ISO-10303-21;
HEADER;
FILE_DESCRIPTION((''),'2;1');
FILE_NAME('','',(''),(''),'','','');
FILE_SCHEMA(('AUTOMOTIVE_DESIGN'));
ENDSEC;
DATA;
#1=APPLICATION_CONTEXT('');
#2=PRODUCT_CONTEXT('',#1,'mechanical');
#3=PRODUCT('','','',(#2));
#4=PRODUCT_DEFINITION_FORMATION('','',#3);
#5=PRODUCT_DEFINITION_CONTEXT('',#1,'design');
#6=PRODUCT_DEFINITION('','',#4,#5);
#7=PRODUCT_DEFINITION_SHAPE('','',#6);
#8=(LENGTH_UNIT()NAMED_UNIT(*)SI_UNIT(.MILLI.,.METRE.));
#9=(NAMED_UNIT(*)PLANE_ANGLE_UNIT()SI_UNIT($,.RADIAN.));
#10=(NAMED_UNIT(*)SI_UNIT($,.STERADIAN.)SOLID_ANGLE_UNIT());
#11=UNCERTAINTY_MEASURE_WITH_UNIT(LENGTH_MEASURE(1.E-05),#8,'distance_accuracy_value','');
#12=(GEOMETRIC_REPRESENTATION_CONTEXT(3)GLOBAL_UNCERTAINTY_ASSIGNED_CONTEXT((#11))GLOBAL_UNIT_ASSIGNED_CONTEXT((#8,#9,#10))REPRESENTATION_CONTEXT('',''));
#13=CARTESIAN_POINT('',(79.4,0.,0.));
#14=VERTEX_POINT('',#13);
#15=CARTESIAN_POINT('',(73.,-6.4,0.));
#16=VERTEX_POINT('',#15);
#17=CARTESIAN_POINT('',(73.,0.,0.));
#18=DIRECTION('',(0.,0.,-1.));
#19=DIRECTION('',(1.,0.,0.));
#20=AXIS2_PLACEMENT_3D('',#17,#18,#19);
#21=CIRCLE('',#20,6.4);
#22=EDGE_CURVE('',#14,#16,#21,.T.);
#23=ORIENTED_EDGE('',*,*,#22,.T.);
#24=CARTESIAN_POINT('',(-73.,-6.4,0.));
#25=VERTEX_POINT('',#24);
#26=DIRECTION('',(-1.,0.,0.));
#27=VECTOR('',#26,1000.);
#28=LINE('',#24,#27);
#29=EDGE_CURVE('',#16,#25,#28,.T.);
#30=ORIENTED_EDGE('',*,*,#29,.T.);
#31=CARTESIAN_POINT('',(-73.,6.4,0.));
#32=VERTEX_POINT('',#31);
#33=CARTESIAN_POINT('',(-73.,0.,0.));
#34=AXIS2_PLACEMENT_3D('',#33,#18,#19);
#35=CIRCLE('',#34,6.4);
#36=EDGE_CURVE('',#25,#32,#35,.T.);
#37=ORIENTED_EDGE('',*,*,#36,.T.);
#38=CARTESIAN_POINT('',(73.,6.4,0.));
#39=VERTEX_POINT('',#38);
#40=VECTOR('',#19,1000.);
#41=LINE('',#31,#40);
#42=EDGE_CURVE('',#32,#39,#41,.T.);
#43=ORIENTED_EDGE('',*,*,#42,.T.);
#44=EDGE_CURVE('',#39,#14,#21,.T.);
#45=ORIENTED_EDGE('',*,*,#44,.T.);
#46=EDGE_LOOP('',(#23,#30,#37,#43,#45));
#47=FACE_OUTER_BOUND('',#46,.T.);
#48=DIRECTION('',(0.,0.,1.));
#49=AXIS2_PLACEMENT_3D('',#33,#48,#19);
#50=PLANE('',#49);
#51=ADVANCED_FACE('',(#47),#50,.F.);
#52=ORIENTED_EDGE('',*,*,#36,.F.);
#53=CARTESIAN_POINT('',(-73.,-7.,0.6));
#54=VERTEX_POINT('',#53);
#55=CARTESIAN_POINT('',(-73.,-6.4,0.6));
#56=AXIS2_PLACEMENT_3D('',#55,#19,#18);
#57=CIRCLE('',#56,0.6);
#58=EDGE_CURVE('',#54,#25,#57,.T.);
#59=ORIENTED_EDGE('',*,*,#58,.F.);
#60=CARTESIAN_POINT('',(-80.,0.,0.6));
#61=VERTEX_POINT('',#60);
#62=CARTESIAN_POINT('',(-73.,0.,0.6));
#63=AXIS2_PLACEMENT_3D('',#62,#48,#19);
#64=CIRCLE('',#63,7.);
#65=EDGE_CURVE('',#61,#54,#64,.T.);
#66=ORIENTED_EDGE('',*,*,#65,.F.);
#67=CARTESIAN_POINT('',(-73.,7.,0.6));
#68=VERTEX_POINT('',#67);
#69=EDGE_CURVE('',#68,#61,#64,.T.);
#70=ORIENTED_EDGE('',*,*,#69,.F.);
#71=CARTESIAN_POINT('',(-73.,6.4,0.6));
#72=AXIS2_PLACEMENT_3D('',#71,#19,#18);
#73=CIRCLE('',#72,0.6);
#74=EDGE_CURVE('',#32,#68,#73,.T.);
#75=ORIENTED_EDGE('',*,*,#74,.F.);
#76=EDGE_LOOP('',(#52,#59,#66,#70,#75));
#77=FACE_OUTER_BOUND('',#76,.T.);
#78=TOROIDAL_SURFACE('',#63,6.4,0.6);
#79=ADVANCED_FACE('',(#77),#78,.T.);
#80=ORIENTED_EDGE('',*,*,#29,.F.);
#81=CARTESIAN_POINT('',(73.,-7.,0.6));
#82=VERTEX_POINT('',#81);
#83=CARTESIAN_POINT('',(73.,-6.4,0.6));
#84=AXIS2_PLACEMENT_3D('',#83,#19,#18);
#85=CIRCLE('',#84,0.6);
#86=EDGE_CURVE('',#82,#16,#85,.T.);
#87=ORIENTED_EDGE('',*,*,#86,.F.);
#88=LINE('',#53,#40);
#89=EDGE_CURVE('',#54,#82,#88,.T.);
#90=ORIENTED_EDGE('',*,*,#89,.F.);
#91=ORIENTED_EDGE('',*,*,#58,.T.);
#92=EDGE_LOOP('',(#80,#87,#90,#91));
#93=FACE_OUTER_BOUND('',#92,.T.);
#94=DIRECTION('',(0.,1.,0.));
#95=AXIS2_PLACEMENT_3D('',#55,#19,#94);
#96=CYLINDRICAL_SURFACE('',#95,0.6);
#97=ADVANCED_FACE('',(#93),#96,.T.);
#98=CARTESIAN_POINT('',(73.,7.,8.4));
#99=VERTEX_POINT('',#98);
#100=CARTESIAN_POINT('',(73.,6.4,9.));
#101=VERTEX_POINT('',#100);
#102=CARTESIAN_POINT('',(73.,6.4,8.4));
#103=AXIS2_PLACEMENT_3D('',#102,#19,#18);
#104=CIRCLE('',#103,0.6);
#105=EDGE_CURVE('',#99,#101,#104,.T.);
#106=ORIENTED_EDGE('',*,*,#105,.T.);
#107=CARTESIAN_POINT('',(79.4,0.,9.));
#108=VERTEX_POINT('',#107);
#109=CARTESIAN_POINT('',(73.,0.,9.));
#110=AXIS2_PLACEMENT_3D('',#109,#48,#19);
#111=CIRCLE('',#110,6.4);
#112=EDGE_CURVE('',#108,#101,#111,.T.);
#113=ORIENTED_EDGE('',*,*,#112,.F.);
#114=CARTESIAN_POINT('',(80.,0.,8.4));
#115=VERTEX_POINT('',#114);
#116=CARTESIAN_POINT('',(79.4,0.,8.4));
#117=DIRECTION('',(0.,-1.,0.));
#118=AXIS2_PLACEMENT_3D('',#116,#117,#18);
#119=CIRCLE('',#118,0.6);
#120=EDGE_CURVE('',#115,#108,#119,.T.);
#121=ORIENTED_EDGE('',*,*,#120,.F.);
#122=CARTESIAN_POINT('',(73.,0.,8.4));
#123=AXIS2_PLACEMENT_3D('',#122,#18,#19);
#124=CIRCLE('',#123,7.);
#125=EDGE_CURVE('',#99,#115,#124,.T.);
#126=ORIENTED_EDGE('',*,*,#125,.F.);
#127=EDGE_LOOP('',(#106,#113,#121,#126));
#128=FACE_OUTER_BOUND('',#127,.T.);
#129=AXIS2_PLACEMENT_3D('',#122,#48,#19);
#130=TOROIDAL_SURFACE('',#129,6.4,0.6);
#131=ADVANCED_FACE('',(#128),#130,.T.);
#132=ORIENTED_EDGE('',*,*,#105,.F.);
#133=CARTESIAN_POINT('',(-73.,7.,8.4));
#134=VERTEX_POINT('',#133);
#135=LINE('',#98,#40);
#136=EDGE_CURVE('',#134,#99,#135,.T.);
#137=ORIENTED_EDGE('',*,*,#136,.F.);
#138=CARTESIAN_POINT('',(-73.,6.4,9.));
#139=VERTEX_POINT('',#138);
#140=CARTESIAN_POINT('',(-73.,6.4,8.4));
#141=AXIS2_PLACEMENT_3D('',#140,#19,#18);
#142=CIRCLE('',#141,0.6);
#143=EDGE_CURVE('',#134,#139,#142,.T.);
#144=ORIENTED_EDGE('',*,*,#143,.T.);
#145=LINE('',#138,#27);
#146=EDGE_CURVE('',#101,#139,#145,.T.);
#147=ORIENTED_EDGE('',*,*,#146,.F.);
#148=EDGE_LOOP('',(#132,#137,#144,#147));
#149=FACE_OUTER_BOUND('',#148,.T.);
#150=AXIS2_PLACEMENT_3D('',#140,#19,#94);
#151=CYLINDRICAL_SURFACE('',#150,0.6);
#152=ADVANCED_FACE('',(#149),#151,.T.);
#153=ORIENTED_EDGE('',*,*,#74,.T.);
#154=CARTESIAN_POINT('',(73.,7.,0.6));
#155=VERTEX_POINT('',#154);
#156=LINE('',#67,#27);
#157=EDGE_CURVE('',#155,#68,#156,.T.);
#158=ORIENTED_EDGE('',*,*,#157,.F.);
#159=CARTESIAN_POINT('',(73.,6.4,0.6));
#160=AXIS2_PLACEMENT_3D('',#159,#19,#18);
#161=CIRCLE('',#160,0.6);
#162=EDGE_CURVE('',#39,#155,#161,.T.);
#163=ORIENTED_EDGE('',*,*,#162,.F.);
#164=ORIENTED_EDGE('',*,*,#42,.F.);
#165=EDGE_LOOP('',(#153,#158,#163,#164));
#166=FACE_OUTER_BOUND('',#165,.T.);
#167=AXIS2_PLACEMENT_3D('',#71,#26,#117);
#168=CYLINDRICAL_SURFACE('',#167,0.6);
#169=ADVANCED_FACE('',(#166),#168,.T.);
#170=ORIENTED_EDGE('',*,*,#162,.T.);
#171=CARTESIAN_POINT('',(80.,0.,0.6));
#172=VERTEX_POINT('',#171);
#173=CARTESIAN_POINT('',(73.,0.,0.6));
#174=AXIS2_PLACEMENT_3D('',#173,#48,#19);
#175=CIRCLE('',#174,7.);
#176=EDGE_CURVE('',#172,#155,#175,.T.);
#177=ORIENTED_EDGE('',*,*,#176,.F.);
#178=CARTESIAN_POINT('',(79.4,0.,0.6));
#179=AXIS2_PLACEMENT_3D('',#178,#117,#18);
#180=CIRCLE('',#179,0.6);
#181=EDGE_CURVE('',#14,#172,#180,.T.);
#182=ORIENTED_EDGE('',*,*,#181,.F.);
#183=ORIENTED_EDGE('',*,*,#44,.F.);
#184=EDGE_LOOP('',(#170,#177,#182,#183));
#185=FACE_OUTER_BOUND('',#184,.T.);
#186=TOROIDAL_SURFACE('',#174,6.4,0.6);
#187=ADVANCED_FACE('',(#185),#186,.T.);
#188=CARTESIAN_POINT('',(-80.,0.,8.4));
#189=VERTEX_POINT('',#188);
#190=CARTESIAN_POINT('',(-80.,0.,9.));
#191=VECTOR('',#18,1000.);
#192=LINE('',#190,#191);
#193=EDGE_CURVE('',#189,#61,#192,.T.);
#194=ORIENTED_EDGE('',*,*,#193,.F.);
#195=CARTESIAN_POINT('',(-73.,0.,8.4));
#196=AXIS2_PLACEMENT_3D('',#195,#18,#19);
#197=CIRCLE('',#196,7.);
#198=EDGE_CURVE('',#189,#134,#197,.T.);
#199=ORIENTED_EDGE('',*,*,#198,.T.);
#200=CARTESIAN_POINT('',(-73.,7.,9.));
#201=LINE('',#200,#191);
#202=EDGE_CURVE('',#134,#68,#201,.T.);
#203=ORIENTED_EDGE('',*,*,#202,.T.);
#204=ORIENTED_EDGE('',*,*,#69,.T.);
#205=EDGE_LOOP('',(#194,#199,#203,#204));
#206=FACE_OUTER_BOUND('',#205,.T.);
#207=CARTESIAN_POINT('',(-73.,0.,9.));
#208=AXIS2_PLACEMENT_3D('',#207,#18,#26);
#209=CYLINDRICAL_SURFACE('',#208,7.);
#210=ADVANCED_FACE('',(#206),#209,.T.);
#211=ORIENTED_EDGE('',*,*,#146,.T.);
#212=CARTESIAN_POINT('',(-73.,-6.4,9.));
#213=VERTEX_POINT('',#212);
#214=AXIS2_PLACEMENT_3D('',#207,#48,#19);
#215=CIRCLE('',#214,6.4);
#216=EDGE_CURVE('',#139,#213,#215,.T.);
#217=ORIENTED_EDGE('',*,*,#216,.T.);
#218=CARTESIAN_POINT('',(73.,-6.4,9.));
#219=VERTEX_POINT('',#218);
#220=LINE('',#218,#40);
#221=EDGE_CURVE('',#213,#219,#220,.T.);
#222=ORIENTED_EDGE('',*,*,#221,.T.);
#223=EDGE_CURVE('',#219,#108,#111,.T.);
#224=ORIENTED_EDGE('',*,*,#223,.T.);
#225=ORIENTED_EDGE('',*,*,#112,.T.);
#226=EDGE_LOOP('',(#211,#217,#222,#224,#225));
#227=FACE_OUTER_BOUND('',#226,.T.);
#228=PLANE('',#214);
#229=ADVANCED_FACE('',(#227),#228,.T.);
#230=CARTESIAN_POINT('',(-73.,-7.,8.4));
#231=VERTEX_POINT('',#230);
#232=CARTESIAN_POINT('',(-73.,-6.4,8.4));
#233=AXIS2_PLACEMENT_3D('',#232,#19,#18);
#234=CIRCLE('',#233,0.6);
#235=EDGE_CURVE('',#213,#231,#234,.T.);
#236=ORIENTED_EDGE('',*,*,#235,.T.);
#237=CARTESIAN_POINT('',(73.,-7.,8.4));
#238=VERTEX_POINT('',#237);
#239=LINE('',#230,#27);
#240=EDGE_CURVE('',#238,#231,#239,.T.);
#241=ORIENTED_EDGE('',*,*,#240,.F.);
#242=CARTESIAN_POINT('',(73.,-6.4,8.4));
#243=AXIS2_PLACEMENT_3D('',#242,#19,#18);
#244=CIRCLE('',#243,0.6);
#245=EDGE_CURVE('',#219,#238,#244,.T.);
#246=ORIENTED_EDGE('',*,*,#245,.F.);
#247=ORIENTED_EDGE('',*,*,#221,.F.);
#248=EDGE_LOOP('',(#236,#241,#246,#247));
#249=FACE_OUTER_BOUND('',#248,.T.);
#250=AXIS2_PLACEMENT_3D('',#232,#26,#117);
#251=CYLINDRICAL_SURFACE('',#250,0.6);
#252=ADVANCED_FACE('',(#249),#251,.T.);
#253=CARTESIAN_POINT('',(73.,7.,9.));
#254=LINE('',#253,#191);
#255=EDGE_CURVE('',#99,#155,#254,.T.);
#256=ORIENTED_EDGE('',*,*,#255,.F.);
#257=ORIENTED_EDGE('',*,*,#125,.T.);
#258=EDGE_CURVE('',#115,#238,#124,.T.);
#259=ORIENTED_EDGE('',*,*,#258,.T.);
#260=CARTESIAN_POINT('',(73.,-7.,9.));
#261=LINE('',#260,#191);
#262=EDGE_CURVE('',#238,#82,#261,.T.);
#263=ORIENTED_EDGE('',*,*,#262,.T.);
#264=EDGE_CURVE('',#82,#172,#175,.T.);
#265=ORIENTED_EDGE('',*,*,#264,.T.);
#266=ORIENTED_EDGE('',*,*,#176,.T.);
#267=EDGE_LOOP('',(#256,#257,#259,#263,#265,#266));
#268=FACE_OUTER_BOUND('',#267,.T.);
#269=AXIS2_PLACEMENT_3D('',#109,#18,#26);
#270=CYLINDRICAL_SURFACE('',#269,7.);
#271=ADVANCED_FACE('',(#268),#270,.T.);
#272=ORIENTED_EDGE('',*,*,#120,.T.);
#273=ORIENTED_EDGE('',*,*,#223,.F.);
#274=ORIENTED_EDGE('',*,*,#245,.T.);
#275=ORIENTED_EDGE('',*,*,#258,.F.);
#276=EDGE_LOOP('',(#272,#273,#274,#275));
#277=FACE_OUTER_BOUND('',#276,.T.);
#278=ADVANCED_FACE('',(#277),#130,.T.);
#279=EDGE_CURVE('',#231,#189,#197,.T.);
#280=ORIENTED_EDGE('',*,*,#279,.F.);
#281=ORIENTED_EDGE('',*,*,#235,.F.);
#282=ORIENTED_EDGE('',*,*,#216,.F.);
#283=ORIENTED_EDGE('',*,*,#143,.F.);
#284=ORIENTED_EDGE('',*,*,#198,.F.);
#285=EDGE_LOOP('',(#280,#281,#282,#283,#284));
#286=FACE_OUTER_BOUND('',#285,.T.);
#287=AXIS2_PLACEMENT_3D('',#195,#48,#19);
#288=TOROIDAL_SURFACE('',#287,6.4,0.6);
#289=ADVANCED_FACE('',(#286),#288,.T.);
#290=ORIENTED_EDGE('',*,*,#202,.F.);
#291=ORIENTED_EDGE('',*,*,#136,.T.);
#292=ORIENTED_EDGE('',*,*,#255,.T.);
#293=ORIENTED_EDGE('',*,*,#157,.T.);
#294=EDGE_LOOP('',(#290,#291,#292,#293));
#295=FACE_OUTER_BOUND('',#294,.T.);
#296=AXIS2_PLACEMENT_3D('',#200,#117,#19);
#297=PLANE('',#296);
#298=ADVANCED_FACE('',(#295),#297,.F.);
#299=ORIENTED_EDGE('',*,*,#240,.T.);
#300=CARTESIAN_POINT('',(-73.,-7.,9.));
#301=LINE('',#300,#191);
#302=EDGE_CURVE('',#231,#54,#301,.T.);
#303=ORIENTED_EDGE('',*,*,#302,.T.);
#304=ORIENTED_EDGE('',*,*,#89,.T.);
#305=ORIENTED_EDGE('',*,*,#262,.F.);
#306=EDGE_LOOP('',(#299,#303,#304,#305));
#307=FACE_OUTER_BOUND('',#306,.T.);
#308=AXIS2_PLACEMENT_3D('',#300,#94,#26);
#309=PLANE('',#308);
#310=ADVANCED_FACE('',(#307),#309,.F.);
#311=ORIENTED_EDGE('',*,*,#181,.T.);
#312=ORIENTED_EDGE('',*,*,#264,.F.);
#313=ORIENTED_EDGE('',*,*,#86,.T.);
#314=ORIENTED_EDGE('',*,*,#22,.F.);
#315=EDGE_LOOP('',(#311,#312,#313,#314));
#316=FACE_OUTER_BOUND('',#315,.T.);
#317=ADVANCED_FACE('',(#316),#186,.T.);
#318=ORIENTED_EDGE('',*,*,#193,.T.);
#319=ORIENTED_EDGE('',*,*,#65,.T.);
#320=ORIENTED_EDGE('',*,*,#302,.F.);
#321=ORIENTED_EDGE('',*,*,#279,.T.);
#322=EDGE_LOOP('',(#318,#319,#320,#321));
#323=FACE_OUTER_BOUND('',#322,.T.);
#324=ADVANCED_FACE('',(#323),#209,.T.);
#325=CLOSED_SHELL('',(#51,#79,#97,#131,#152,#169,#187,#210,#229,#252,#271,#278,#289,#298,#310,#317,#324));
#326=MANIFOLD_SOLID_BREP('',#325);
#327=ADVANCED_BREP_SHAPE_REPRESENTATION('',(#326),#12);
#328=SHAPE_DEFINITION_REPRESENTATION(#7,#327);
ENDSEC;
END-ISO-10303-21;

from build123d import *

# Parameters (mm, degrees)
BASE_EXTRUDE_DEPTH = 9
FILLET1_R          = 0.6


with BuildPart() as part:
    # Sketch1 → Base-Extrude (new body)
    with BuildSketch(Plane.XY):
        with BuildLine():
            Line((-73, 7), (73, 7))
            ThreePointArc((73, 7), (80, 0), (73, -7))
            Line((73, -7), (-73, -7))
            ThreePointArc((-73, -7), (-80, 0), (-73, 7))
        make_face()
    extrude(amount=BASE_EXTRUDE_DEPTH)

    # Fillet1
    fillet1_edges = [part.edges().sort_by_distance(p)[0] for p in [
        (80, 0, 9),
        (0, 7, 9),
        (-80, 0, 9),
        (0, 7, 0),
        (80, 0, 0),
        (0, -7, 0),
        (-80, 0, 0),
        (0, -7, 9),
    ]]
    fillet(fillet1_edges, radius=FILLET1_R)


solid = part.part
